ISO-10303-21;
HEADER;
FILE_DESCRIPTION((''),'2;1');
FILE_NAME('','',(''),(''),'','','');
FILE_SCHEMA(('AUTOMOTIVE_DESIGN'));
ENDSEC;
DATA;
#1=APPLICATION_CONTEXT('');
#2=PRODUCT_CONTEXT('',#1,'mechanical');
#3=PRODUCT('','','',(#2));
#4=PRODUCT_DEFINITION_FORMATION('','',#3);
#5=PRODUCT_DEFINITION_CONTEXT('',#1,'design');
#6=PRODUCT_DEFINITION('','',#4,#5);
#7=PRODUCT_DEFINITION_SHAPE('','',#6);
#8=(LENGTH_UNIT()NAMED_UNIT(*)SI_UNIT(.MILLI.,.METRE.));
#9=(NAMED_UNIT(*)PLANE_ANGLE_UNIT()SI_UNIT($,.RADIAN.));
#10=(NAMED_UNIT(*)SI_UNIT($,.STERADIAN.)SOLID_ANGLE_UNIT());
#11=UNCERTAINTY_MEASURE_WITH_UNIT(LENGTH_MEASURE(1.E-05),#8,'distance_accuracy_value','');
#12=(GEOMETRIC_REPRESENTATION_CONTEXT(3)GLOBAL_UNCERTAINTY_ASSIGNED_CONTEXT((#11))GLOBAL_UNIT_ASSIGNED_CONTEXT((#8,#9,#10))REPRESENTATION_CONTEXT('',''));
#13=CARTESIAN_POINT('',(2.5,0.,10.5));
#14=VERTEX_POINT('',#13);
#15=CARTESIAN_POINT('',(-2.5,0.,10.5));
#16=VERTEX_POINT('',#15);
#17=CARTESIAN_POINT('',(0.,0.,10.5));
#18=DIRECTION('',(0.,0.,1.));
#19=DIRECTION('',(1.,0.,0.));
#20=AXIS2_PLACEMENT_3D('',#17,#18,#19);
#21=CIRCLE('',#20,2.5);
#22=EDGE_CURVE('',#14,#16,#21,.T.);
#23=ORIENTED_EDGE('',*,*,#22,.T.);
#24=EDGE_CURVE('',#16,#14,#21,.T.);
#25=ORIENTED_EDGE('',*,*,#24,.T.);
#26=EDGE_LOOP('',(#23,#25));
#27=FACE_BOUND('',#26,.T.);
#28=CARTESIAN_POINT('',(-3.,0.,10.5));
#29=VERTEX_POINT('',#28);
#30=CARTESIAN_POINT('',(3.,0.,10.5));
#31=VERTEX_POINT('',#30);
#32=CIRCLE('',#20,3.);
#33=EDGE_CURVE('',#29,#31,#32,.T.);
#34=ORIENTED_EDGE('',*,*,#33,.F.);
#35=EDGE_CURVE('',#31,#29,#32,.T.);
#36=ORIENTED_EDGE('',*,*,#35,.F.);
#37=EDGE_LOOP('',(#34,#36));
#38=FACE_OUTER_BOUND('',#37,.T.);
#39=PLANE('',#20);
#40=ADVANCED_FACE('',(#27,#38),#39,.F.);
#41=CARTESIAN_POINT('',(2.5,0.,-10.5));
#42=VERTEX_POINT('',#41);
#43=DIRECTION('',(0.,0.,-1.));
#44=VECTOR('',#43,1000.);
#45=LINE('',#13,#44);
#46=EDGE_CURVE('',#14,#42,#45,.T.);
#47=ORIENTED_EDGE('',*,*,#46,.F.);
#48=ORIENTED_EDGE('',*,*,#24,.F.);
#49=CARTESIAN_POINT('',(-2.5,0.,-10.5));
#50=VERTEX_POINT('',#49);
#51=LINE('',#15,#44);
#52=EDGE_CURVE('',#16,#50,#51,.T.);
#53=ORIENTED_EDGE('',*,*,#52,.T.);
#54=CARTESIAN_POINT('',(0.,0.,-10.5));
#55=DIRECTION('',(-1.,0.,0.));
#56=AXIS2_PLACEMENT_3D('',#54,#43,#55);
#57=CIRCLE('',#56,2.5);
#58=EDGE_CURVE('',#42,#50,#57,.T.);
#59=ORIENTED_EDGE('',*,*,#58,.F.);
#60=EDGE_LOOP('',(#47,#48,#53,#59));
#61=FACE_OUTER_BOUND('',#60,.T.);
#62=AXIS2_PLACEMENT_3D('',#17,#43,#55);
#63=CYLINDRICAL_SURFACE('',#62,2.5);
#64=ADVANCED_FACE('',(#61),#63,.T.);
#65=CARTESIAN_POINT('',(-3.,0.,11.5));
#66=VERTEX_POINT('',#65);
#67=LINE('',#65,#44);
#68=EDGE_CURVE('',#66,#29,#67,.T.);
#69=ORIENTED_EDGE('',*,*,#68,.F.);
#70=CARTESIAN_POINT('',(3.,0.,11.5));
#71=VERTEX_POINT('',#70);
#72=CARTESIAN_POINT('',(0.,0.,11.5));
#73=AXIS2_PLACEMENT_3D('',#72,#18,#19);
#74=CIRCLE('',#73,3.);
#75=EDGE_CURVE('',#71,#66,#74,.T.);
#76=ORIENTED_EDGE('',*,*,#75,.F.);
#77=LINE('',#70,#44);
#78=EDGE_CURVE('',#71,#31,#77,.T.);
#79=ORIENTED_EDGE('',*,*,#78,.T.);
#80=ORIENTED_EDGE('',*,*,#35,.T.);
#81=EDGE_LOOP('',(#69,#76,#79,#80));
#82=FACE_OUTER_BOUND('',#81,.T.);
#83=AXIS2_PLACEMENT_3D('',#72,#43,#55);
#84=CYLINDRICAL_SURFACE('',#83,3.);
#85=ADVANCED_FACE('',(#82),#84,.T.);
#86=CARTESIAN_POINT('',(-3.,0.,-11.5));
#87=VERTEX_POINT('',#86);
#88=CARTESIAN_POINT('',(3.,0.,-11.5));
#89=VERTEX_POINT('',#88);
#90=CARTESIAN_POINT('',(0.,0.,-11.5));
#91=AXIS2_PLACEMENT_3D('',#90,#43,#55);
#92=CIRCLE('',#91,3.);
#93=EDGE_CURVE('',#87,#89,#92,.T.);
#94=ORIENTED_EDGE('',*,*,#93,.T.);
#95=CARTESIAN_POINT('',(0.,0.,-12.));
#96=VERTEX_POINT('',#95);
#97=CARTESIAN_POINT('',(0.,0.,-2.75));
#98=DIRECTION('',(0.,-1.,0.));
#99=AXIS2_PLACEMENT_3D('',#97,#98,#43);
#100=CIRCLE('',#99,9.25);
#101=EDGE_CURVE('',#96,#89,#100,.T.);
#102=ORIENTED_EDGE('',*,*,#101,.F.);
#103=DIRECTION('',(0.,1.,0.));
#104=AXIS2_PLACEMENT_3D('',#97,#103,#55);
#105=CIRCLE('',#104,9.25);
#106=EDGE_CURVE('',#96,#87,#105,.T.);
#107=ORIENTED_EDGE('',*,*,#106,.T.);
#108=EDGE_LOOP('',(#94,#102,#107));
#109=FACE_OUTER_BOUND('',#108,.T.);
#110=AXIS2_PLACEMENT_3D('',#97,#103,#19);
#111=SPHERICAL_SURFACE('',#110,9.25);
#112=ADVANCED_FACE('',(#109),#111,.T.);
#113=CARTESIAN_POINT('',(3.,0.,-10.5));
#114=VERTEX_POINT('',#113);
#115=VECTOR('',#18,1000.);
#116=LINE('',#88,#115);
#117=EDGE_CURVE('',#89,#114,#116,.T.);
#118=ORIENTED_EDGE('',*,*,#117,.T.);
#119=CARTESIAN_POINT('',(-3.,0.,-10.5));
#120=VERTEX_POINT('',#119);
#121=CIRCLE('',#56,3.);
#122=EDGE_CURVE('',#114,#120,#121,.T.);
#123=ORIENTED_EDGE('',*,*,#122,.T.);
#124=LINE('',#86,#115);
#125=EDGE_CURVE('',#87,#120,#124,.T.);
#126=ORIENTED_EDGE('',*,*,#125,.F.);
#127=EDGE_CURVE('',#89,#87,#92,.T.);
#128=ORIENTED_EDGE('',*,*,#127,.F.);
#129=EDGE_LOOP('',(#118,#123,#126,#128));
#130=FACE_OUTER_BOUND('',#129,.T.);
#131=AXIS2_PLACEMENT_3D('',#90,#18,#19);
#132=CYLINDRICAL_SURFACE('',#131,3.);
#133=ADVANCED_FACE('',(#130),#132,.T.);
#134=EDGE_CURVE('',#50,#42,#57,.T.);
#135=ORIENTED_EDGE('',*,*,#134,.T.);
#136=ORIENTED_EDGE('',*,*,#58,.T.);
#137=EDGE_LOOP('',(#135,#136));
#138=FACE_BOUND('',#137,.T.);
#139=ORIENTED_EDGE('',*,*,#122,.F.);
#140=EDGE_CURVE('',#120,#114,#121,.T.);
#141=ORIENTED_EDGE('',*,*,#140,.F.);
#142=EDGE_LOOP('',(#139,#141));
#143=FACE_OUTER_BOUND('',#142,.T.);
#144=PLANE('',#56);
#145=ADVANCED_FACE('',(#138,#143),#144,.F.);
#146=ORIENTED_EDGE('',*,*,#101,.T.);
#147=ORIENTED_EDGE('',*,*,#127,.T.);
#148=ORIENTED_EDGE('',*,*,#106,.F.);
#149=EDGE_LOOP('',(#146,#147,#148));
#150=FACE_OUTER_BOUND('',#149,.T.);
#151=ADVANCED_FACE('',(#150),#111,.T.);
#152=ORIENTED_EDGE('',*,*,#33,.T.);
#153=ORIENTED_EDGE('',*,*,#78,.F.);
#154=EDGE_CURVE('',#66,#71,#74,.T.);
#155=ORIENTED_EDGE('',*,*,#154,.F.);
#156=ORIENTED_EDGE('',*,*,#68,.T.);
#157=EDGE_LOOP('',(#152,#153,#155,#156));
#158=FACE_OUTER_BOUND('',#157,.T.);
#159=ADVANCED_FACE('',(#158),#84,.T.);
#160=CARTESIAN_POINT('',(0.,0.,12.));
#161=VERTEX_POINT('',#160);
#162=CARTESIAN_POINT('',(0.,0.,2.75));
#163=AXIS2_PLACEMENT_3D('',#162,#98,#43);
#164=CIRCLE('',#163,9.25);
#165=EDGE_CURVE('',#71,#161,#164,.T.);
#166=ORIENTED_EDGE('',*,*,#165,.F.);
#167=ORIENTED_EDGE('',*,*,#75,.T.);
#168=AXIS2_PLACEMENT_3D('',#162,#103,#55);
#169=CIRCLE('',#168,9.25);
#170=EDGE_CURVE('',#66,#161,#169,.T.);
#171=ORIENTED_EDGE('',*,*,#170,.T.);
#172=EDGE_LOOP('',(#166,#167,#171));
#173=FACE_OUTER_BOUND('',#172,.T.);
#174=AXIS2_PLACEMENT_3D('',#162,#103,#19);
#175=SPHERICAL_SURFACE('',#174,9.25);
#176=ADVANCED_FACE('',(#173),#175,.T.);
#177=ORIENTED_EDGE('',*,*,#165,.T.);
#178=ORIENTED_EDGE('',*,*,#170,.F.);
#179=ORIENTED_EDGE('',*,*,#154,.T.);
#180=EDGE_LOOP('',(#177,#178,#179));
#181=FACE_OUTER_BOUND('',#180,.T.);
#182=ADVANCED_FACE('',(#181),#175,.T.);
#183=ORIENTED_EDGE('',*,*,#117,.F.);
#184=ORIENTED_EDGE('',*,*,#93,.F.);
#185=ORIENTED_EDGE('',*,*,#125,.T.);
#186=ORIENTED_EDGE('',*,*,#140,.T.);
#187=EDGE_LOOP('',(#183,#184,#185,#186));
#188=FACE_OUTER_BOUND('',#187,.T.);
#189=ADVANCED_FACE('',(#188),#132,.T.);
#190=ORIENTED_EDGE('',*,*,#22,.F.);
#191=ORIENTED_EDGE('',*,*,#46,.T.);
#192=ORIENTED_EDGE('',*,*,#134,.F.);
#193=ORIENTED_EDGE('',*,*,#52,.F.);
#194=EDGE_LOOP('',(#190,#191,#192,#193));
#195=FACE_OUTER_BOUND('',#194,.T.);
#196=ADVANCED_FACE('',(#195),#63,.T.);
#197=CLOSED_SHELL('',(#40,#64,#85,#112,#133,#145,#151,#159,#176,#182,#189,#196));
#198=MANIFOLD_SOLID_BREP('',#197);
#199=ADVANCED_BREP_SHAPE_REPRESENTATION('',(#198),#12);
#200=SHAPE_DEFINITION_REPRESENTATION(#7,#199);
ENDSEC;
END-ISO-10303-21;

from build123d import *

# Parameters (mm, degrees)
SKETCH1_R           = 2.5
BOSS_EXTRUDE1_DEPTH = 10.5
SKETCH2_R           = 3
BOSS_EXTRUDE2_DEPTH = 1
BOSS_EXTRUDE3_START = 1
SKETCH3_R           = 3
BOSS_EXTRUDE3_DEPTH = 1
DOME1_FACE_RADIUS   = 3
DOME1_HEIGHT        = 0.5
DOME2_FACE_RADIUS   = 3
DOME2_HEIGHT        = 0.5


with BuildPart() as part:
    # Sketch1 → Boss-Extrude1 (new, symmetric)
    with BuildSketch(Plane.XY):
        with Locations(Location((0, 0, 0), (0, 0, 180))):
            Circle(SKETCH1_R)
    extrude(amount=BOSS_EXTRUDE1_DEPTH, both=True)

    # Sketch2 → Boss-Extrude2 (add)
    with BuildSketch(Plane(origin=(0, 0, -10.5), x_dir=(-1, 0, 0), z_dir=(0, 0, -1))):
        Circle(SKETCH2_R)
    extrude(amount=BOSS_EXTRUDE2_DEPTH)

    # Sketch3 → Boss-Extrude3 (add)
    with BuildSketch(Plane.XY.offset(10.5).offset(BOSS_EXTRUDE3_START)):
        with Locations(Location((0, 0, 0), (0, 0, 180))):
            Circle(SKETCH3_R)
    extrude(amount=-BOSS_EXTRUDE3_DEPTH)

    # Dome1: a dome of height H over a round flat face of radius A is a cap of a sphere of radius (A * A + H * H) / (2 * H)
    dome1_r = (DOME1_FACE_RADIUS * DOME1_FACE_RADIUS + DOME1_HEIGHT * DOME1_HEIGHT) / (2 * DOME1_HEIGHT)
    dome1_base = Plane((0, 0, -11.5), z_dir=(0, 0, -1))
    with Locations(dome1_base.offset(DOME1_HEIGHT - dome1_r)):
        dome1_ball = Sphere(dome1_r, mode=Mode.PRIVATE)
    add(split(dome1_ball, bisect_by=dome1_base, keep=Keep.TOP, mode=Mode.PRIVATE))

    # Dome2: a dome of height H over a round flat face of radius A is a cap of a sphere of radius (A * A + H * H) / (2 * H)
    dome2_r = (DOME2_FACE_RADIUS * DOME2_FACE_RADIUS + DOME2_HEIGHT * DOME2_HEIGHT) / (2 * DOME2_HEIGHT)
    dome2_base = Plane((0, 0, 11.5), z_dir=(0, 0, 1))
    with Locations(dome2_base.offset(DOME2_HEIGHT - dome2_r)):
        dome2_ball = Sphere(dome2_r, mode=Mode.PRIVATE)
    add(split(dome2_ball, bisect_by=dome2_base, keep=Keep.TOP, mode=Mode.PRIVATE))


solid = part.part
